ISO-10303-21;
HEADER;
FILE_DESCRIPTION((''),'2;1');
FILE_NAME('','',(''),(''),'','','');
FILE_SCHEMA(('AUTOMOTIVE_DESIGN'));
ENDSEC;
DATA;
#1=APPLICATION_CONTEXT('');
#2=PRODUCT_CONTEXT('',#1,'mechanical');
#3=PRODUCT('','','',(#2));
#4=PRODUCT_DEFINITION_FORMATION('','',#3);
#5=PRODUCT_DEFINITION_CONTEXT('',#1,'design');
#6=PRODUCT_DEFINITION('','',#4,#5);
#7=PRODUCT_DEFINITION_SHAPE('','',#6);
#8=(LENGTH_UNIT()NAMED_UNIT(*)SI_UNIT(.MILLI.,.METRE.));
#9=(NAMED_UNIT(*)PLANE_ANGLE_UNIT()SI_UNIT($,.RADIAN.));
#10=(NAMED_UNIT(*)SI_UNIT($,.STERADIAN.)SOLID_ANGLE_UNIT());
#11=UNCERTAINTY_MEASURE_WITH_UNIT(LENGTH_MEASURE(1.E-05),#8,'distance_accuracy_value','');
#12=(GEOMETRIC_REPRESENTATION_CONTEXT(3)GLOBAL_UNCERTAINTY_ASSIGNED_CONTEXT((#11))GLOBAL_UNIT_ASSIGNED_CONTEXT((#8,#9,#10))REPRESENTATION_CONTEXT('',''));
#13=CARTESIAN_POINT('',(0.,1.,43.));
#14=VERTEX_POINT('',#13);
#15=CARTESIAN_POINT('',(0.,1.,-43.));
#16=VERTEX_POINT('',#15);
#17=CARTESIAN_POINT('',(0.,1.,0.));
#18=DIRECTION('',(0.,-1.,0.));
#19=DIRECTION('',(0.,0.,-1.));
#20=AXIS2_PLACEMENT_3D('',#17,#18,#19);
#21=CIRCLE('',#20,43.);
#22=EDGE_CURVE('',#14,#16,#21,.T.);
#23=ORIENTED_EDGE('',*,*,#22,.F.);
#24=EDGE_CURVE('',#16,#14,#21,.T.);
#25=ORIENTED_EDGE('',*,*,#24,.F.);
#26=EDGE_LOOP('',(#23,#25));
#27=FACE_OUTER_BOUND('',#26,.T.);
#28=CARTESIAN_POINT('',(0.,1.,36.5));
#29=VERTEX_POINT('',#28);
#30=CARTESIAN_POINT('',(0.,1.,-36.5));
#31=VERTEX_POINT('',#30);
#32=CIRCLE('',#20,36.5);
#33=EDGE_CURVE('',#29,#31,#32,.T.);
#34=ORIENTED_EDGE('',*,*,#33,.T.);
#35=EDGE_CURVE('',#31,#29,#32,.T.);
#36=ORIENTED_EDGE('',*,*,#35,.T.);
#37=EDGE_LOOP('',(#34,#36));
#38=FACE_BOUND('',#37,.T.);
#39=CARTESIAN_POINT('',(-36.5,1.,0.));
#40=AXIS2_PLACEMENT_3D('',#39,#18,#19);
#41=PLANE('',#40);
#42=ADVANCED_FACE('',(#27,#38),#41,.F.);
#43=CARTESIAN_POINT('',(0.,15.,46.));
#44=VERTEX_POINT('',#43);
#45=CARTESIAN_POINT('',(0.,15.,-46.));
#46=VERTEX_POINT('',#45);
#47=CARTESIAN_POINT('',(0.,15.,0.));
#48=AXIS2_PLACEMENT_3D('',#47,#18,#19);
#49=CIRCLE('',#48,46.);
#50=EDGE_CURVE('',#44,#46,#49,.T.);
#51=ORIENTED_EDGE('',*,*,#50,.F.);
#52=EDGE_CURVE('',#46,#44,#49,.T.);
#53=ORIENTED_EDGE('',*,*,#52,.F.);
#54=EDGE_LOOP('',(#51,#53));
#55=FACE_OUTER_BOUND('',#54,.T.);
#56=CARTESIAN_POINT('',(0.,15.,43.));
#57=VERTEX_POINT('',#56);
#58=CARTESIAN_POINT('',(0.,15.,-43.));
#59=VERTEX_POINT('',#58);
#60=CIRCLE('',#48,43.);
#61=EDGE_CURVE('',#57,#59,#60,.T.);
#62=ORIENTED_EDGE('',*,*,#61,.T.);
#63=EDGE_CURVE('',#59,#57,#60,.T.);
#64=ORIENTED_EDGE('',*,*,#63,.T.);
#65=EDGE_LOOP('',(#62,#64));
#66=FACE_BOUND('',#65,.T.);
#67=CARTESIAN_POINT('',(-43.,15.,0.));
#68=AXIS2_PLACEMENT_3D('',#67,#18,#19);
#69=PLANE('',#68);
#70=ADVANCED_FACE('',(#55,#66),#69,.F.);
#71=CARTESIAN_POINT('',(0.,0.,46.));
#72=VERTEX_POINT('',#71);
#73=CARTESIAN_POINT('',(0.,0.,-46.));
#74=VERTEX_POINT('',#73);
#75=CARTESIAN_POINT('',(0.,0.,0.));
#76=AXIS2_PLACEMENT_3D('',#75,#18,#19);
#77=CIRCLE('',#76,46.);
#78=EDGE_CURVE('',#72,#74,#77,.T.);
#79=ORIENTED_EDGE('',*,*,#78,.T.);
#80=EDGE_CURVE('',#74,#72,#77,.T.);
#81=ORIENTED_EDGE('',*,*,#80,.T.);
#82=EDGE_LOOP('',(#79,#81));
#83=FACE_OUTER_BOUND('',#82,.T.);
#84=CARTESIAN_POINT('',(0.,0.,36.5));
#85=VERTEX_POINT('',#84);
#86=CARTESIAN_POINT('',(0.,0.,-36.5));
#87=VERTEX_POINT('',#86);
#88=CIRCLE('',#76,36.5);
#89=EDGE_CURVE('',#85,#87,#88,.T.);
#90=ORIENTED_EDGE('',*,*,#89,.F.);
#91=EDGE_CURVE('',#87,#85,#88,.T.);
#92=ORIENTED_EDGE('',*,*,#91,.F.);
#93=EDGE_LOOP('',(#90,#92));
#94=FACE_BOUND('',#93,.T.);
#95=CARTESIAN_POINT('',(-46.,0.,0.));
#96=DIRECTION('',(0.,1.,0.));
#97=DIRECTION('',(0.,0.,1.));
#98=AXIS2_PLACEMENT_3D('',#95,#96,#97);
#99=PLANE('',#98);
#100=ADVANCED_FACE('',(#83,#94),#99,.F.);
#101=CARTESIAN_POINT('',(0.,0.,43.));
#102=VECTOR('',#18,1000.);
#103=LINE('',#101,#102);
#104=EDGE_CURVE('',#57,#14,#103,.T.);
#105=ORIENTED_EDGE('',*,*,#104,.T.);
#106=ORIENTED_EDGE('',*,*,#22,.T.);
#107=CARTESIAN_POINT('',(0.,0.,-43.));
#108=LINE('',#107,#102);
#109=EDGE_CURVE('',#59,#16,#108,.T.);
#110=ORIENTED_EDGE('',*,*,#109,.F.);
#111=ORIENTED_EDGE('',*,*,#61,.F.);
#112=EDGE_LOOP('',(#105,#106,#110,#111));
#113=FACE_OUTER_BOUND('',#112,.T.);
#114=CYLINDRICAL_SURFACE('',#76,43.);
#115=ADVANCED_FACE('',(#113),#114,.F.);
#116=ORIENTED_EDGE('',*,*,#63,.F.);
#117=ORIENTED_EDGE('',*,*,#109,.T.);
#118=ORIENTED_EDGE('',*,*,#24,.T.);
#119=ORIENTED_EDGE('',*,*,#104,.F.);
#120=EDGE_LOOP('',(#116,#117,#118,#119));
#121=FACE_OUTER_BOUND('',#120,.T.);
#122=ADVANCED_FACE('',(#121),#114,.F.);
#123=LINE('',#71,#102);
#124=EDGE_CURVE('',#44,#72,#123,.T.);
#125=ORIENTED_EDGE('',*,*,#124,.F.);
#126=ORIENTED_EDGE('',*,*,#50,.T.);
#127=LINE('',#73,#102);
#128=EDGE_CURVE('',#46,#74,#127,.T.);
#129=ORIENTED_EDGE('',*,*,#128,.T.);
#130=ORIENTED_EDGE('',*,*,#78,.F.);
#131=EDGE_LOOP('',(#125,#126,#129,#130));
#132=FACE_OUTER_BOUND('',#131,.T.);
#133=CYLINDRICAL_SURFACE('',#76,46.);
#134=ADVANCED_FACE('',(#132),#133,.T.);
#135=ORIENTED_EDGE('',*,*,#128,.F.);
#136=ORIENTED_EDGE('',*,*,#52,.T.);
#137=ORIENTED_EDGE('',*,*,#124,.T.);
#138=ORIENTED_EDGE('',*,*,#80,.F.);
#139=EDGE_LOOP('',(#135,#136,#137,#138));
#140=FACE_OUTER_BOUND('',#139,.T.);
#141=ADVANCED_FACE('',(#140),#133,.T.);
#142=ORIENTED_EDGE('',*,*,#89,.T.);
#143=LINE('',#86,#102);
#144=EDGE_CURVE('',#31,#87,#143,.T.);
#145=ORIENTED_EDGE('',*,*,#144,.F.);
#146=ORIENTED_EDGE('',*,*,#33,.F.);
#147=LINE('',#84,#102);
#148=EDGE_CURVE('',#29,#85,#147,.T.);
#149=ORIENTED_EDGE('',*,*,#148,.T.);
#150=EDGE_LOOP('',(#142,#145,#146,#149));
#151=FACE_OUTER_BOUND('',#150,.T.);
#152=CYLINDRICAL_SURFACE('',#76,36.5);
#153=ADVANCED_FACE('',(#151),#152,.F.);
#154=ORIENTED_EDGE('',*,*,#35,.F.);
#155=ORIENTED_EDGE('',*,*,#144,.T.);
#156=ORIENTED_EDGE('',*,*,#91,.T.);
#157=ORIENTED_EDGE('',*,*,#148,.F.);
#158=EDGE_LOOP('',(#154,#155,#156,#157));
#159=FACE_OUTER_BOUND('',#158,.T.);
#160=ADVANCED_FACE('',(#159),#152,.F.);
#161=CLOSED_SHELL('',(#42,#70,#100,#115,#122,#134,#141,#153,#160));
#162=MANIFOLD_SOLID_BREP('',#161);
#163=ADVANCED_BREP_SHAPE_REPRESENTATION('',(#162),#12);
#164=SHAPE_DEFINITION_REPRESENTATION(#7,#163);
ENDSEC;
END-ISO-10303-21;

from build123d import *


with BuildPart() as part:
    # 草图1 → 旋转1 (revolve)
    with BuildSketch(Plane.XY, mode=Mode.PRIVATE) as revolve_1_sk:
        Polygon((-46, 15), (-46, 0), (-36.5, 0), (-36.5, 1), (-43, 1), (-43, 15), align=None)
    revolve(revolve_1_sk.sketch.rotate(Axis((0, 0, 0), (0, 1, 0)), 270), axis=Axis((0, 0, 0), (0, 1, 0)))


solid = part.part
